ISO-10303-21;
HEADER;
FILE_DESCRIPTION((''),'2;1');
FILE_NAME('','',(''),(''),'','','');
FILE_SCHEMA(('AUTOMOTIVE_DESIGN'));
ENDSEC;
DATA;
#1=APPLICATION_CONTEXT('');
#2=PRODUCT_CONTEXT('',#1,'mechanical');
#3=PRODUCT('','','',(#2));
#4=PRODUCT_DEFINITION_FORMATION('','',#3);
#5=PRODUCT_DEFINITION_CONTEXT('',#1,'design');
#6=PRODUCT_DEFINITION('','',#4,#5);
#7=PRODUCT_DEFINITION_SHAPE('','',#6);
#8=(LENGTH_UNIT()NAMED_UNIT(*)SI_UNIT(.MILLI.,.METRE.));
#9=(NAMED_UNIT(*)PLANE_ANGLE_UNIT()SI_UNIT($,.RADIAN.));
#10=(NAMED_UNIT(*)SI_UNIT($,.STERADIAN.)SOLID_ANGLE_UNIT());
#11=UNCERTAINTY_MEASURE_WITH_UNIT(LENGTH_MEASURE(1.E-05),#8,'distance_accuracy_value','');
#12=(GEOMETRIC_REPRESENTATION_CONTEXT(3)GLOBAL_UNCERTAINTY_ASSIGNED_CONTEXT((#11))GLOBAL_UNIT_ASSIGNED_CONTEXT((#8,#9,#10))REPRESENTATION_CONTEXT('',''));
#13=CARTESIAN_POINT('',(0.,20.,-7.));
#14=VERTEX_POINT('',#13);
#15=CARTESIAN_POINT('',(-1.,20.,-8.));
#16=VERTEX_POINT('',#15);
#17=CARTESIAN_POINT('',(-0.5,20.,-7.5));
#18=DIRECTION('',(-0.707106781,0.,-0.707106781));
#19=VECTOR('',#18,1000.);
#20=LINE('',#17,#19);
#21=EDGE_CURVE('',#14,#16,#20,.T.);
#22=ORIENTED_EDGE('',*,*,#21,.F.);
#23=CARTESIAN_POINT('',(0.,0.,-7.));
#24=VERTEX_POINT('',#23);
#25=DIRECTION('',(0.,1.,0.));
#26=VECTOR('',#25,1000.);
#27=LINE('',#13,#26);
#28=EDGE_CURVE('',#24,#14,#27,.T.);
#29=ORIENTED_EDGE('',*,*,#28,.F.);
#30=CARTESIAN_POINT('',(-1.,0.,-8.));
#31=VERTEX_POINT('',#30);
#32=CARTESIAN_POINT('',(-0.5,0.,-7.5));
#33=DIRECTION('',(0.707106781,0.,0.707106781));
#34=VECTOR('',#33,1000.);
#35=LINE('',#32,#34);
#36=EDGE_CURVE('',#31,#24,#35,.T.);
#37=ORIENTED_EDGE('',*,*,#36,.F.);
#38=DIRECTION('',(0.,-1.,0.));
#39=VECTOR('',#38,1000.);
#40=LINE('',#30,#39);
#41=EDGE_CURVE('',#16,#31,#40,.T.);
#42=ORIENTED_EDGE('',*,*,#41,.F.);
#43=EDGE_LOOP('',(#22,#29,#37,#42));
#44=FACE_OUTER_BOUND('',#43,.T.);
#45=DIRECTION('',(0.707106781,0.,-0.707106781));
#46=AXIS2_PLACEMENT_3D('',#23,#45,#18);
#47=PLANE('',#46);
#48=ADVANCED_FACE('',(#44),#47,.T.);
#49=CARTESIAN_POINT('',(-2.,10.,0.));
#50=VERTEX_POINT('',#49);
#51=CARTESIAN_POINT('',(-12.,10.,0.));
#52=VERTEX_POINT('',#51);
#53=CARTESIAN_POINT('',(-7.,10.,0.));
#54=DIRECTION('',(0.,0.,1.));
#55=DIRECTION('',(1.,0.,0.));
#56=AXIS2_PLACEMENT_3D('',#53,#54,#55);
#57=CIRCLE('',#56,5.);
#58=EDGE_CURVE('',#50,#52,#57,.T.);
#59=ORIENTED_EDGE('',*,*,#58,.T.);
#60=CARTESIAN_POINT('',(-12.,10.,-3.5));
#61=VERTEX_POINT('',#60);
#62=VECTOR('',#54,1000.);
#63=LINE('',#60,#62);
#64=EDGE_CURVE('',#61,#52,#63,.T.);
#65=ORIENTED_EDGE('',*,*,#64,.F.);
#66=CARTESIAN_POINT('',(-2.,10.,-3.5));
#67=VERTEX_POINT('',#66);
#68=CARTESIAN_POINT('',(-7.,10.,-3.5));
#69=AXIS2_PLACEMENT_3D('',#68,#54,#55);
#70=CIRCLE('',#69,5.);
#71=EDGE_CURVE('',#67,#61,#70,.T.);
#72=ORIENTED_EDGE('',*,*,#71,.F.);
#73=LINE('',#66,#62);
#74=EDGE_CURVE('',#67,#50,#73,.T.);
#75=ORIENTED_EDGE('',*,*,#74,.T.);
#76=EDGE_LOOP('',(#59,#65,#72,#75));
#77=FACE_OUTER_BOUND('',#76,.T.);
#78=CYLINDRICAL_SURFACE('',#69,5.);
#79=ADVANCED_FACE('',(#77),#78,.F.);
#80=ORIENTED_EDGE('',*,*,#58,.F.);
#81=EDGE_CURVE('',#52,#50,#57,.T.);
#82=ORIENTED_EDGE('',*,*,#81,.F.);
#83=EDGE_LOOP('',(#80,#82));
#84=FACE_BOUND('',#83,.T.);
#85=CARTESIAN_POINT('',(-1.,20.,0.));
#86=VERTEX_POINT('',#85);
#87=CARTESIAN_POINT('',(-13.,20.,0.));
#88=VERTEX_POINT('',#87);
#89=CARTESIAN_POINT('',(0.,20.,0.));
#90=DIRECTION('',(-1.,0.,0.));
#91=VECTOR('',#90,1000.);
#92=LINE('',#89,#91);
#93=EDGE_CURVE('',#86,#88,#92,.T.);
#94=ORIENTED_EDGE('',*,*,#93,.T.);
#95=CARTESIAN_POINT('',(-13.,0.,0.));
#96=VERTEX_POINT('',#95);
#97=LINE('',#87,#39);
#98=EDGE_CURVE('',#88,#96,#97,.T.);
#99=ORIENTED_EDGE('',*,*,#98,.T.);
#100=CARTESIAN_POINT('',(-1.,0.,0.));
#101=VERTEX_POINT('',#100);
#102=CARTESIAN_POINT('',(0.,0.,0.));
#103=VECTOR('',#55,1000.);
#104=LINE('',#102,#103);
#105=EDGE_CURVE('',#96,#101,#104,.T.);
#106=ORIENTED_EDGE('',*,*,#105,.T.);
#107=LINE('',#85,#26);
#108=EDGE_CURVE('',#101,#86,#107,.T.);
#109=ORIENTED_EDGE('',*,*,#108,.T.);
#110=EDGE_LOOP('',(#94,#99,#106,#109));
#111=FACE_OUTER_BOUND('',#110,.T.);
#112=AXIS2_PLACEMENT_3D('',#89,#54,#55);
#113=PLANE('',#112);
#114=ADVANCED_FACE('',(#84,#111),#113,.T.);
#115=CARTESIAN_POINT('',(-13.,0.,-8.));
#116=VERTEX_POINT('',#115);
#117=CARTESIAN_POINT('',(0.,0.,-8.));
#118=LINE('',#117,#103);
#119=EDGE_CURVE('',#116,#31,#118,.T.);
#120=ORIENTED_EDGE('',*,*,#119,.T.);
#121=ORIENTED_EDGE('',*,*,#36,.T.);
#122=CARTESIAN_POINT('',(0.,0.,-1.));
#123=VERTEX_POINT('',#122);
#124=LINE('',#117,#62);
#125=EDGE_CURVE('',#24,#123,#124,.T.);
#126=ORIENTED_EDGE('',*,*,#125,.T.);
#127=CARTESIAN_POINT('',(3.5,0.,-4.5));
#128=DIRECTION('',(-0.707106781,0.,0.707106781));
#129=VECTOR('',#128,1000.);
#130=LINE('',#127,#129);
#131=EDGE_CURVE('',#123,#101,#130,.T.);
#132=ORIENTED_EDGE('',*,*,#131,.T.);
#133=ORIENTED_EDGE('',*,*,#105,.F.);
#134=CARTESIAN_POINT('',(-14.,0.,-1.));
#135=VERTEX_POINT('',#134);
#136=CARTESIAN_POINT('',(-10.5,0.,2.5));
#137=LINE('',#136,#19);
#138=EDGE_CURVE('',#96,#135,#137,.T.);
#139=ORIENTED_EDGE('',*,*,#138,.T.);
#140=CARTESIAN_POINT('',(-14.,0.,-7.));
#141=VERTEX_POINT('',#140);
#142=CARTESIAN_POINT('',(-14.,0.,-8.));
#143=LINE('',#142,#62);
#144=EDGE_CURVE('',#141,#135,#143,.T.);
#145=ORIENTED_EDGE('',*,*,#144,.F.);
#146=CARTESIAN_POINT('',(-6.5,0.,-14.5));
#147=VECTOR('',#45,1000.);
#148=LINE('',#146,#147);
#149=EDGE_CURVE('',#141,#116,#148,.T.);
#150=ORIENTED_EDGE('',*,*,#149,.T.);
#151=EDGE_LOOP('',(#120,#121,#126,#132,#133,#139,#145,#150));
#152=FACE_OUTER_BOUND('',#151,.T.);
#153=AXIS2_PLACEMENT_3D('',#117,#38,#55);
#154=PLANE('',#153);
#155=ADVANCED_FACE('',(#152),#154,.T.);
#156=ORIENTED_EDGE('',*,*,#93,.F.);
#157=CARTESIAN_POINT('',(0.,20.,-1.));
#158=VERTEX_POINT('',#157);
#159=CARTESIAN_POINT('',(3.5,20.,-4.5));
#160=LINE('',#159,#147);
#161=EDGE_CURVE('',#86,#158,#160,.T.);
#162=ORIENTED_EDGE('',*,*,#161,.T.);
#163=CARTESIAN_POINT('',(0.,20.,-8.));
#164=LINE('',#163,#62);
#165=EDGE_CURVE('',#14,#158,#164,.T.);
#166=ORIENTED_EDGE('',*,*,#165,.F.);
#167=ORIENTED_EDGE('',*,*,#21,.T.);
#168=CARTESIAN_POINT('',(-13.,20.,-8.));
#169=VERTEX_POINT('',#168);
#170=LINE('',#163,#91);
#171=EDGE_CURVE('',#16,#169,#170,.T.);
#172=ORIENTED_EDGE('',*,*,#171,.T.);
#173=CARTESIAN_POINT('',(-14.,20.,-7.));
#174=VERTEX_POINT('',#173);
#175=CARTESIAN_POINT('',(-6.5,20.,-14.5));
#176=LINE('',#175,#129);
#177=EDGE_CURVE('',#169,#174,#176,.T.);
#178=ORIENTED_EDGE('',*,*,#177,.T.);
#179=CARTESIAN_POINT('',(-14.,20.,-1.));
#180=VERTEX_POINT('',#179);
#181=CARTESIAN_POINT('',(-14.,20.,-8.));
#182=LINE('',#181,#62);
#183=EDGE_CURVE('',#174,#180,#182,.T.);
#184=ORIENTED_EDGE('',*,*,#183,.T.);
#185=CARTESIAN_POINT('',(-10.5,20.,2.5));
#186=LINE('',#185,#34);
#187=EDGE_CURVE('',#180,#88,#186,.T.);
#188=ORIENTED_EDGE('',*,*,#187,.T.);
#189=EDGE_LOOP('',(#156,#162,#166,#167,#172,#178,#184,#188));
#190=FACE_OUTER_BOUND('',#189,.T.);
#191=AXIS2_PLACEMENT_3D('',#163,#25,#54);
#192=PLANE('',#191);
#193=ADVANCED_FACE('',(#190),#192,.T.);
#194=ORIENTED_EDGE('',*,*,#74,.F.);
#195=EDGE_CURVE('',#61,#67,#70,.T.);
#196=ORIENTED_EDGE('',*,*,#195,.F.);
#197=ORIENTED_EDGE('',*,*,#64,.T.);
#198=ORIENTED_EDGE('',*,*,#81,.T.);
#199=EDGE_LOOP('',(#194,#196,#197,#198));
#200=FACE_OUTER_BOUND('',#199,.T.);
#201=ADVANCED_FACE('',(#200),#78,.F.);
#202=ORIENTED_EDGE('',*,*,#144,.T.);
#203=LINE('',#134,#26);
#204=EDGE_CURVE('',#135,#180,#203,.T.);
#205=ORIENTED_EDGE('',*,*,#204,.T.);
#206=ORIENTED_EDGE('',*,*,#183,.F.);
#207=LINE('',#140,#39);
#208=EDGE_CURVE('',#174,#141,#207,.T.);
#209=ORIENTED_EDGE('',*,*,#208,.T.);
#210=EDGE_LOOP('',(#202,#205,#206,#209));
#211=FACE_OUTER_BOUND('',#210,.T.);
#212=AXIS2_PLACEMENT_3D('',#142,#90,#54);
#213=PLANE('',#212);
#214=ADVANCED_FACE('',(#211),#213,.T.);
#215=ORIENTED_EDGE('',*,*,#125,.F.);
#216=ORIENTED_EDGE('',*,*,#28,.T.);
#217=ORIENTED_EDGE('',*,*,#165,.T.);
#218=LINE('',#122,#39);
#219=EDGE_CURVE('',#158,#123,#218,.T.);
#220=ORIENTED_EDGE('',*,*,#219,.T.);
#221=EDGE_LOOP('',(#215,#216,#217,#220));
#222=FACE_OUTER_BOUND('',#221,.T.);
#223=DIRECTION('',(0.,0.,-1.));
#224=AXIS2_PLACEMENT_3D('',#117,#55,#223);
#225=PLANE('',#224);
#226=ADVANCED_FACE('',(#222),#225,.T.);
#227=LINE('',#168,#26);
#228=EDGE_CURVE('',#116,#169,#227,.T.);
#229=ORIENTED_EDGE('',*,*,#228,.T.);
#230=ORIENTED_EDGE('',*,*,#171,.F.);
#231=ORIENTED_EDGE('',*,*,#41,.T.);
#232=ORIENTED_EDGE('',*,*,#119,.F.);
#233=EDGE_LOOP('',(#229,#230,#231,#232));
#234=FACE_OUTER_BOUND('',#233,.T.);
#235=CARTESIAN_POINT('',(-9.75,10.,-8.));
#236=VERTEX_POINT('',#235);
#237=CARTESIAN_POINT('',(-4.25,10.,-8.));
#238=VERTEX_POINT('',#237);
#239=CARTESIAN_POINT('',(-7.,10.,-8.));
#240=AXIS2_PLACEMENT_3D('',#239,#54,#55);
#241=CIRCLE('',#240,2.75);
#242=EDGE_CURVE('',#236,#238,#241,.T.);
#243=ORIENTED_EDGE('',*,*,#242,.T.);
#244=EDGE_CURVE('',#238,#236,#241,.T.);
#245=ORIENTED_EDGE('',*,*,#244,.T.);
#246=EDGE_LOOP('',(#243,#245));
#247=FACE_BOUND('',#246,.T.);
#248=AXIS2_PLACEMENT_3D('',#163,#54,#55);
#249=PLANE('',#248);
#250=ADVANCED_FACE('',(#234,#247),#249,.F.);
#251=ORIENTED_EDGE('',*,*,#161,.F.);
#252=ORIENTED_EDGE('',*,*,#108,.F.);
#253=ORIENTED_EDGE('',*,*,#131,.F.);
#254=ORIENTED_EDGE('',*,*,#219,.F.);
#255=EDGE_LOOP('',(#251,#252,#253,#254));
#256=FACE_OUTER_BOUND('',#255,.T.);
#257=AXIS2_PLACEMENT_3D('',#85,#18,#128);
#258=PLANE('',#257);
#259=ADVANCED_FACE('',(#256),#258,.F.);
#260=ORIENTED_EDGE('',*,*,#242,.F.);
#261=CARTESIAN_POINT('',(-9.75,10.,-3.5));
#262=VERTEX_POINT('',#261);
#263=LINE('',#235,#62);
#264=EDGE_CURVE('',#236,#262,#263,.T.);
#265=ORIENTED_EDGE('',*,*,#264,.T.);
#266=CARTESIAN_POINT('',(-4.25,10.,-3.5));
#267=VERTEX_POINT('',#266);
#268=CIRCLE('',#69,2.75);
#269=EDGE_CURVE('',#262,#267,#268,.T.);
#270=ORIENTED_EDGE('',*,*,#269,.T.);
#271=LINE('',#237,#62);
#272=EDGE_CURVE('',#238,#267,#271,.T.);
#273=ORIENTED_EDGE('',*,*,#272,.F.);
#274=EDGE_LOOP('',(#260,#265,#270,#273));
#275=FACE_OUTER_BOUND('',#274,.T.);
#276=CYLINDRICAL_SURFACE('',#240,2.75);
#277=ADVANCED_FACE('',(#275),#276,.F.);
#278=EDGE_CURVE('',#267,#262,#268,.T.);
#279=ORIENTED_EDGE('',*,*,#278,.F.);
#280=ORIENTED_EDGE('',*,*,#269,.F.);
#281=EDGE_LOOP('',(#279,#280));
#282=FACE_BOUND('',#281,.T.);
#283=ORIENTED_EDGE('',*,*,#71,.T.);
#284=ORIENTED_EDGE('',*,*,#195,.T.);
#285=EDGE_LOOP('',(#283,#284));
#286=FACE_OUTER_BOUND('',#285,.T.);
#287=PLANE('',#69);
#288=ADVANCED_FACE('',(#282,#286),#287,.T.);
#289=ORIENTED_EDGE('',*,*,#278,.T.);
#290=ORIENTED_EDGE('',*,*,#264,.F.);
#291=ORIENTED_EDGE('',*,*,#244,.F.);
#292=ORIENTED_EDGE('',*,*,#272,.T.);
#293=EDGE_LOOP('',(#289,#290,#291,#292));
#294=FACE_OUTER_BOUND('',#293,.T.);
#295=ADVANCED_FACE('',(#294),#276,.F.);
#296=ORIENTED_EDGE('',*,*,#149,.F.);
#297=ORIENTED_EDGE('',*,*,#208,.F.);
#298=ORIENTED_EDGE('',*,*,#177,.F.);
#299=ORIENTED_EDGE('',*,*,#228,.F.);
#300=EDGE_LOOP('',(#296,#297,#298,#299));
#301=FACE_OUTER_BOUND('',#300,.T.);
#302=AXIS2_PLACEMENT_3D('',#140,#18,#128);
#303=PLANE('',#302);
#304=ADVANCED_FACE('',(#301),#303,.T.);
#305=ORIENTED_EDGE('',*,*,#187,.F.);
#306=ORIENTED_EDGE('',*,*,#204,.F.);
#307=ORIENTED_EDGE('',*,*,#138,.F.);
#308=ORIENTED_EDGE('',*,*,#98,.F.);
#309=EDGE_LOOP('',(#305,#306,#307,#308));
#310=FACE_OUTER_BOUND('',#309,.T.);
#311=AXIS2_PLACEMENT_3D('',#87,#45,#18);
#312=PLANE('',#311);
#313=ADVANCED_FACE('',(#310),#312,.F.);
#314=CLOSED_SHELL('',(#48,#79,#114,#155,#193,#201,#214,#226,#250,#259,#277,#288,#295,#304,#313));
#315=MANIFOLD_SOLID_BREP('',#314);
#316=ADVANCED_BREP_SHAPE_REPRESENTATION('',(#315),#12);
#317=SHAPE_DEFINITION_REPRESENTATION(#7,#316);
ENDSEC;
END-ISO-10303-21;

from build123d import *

# Parameters (mm, degrees)
SKETCH1_W          = 14
SKETCH1_H          = 20
BOSS_EXTRUDE_DEPTH = 8
SKETCH2_R          = 5
CUT_EXTRUDE1_DEPTH = 3.5
SKETCH3_R          = 2.75
CUT_EXTRUDE2_DEPTH = 25.824383175
CHAMFER1_SIZE      = 1


with BuildPart() as part:
    # Sketch1 → Boss-Extrude (new body)
    with BuildSketch(Plane.XY):
        with Locations((-7, 10)):
            Rectangle(SKETCH1_W, SKETCH1_H)
    extrude(amount=-BOSS_EXTRUDE_DEPTH)

    # Sketch2 → Cut-Extrude1 (cut)
    with BuildSketch(Plane.XY):
        with Locations((-7, 10)):
            Circle(SKETCH2_R)
    extrude(amount=-CUT_EXTRUDE1_DEPTH, mode=Mode.SUBTRACT)

    # Sketch3 → Cut-Extrude2 (cut, through all)
    with BuildSketch(Plane.XY.offset(-3.5)):
        with Locations((-7, 10)):
            Circle(SKETCH3_R)
    extrude(amount=-CUT_EXTRUDE2_DEPTH, mode=Mode.SUBTRACT)

    # Chamfer1
    chamfer1_edges = [part.edges().sort_by_distance(p)[0] for p in [
        (-14, 10, -8),
        (0, 10, -8),
        (-14, 10, 0),
        (0, 10, 0),
    ]]
    chamfer(chamfer1_edges, length=CHAMFER1_SIZE)


solid = part.part
